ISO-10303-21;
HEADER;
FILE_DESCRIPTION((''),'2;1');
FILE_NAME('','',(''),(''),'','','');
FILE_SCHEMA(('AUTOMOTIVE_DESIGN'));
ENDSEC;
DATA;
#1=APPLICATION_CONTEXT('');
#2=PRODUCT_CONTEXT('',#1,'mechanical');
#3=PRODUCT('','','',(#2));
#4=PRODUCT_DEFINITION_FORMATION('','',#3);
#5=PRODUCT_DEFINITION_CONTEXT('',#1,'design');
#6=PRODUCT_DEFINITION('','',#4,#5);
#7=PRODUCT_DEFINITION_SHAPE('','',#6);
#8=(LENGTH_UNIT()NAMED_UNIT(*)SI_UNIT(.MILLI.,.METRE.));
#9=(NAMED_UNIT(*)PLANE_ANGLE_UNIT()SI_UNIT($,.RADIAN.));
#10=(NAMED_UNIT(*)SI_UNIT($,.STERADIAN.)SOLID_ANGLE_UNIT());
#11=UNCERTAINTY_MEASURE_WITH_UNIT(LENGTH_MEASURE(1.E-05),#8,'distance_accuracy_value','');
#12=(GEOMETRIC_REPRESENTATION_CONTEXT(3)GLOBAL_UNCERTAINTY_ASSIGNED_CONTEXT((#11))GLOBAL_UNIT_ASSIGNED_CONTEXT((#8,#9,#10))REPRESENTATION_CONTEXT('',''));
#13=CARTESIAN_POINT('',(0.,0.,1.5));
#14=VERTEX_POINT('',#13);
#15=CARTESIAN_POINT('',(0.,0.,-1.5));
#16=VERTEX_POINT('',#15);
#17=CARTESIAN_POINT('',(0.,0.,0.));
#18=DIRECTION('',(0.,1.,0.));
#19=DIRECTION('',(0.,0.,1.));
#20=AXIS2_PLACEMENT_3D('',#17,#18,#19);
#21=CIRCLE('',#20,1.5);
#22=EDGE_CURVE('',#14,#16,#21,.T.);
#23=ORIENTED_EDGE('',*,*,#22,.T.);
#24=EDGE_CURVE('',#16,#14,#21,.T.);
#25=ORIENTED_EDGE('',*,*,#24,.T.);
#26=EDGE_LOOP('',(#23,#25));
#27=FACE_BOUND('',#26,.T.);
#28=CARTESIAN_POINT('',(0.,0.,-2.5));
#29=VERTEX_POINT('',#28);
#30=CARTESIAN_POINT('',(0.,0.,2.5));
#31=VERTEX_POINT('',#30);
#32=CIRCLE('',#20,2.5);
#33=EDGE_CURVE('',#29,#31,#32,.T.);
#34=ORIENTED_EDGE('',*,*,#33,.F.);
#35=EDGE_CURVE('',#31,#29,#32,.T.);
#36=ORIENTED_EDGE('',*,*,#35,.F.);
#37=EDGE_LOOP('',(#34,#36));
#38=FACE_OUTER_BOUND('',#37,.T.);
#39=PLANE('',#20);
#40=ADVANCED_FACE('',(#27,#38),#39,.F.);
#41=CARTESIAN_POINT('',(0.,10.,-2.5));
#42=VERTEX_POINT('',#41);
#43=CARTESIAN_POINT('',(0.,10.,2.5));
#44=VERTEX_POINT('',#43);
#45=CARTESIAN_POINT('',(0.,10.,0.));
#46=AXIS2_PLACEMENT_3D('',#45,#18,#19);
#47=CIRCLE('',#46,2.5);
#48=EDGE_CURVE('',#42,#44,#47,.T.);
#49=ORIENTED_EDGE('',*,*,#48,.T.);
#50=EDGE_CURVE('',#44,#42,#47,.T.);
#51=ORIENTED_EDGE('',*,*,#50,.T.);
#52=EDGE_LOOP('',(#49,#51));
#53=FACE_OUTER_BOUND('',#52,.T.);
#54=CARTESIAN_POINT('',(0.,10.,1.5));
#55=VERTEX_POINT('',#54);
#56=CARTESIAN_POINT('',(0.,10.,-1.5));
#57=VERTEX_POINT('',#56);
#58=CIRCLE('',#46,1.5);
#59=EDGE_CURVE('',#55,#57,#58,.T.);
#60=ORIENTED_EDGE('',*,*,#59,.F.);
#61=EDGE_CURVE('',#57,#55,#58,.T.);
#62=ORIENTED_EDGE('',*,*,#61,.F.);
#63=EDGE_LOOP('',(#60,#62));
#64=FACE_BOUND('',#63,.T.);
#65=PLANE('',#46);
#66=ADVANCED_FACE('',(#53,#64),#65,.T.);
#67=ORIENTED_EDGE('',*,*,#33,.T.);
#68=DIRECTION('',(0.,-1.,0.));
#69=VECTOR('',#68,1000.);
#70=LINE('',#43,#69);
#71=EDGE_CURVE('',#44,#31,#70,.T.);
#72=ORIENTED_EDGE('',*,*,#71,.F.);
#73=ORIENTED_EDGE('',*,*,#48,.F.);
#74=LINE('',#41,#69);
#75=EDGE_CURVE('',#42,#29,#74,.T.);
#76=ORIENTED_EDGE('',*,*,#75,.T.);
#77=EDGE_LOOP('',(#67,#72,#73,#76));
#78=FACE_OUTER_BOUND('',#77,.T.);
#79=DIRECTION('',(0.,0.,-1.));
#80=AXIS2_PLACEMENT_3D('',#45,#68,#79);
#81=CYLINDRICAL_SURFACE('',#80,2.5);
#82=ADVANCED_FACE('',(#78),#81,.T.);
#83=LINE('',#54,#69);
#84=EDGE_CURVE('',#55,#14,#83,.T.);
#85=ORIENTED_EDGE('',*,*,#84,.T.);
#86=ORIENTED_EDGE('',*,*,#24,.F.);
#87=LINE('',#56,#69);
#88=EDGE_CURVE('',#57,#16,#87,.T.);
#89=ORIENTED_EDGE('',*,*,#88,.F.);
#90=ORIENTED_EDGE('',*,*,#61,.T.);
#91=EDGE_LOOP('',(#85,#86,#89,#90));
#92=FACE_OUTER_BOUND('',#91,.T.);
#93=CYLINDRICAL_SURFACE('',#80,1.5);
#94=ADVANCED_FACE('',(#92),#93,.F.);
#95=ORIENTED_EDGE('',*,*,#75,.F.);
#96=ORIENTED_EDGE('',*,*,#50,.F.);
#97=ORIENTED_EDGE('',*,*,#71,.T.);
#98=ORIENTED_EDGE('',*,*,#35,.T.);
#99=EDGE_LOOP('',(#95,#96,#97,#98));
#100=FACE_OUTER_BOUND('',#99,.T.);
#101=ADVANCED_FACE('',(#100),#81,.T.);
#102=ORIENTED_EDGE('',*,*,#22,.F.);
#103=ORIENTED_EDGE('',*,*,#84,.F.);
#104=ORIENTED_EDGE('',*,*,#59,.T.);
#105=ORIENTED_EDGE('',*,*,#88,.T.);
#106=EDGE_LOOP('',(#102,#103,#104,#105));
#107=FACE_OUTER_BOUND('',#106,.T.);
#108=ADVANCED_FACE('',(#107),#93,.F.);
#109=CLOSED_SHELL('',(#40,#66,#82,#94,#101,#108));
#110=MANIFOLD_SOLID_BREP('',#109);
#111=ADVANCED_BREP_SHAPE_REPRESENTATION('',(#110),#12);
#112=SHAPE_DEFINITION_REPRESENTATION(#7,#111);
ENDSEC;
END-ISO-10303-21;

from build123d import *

# Parameters (mm, degrees)
SKETCH_1_R      = 2.5
SKETCH_1_R_2    = 1.5
EXTRUDE_1_DEPTH = 10


with BuildPart() as part:
    # 草图1 → 凸台-拉伸1 (new body)
    with BuildSketch(Plane(origin=(0, 0, 0), x_dir=(1, 0, 0), z_dir=(0, 1, 0))):
        with Locations(Location((0, 0, 0), (0, 0, 270))):
            Circle(SKETCH_1_R)
        with Locations(Location((0, 0, 0), (0, 0, 270))):
            Circle(SKETCH_1_R_2, mode=Mode.SUBTRACT)
    extrude(amount=EXTRUDE_1_DEPTH)


solid = part.part
